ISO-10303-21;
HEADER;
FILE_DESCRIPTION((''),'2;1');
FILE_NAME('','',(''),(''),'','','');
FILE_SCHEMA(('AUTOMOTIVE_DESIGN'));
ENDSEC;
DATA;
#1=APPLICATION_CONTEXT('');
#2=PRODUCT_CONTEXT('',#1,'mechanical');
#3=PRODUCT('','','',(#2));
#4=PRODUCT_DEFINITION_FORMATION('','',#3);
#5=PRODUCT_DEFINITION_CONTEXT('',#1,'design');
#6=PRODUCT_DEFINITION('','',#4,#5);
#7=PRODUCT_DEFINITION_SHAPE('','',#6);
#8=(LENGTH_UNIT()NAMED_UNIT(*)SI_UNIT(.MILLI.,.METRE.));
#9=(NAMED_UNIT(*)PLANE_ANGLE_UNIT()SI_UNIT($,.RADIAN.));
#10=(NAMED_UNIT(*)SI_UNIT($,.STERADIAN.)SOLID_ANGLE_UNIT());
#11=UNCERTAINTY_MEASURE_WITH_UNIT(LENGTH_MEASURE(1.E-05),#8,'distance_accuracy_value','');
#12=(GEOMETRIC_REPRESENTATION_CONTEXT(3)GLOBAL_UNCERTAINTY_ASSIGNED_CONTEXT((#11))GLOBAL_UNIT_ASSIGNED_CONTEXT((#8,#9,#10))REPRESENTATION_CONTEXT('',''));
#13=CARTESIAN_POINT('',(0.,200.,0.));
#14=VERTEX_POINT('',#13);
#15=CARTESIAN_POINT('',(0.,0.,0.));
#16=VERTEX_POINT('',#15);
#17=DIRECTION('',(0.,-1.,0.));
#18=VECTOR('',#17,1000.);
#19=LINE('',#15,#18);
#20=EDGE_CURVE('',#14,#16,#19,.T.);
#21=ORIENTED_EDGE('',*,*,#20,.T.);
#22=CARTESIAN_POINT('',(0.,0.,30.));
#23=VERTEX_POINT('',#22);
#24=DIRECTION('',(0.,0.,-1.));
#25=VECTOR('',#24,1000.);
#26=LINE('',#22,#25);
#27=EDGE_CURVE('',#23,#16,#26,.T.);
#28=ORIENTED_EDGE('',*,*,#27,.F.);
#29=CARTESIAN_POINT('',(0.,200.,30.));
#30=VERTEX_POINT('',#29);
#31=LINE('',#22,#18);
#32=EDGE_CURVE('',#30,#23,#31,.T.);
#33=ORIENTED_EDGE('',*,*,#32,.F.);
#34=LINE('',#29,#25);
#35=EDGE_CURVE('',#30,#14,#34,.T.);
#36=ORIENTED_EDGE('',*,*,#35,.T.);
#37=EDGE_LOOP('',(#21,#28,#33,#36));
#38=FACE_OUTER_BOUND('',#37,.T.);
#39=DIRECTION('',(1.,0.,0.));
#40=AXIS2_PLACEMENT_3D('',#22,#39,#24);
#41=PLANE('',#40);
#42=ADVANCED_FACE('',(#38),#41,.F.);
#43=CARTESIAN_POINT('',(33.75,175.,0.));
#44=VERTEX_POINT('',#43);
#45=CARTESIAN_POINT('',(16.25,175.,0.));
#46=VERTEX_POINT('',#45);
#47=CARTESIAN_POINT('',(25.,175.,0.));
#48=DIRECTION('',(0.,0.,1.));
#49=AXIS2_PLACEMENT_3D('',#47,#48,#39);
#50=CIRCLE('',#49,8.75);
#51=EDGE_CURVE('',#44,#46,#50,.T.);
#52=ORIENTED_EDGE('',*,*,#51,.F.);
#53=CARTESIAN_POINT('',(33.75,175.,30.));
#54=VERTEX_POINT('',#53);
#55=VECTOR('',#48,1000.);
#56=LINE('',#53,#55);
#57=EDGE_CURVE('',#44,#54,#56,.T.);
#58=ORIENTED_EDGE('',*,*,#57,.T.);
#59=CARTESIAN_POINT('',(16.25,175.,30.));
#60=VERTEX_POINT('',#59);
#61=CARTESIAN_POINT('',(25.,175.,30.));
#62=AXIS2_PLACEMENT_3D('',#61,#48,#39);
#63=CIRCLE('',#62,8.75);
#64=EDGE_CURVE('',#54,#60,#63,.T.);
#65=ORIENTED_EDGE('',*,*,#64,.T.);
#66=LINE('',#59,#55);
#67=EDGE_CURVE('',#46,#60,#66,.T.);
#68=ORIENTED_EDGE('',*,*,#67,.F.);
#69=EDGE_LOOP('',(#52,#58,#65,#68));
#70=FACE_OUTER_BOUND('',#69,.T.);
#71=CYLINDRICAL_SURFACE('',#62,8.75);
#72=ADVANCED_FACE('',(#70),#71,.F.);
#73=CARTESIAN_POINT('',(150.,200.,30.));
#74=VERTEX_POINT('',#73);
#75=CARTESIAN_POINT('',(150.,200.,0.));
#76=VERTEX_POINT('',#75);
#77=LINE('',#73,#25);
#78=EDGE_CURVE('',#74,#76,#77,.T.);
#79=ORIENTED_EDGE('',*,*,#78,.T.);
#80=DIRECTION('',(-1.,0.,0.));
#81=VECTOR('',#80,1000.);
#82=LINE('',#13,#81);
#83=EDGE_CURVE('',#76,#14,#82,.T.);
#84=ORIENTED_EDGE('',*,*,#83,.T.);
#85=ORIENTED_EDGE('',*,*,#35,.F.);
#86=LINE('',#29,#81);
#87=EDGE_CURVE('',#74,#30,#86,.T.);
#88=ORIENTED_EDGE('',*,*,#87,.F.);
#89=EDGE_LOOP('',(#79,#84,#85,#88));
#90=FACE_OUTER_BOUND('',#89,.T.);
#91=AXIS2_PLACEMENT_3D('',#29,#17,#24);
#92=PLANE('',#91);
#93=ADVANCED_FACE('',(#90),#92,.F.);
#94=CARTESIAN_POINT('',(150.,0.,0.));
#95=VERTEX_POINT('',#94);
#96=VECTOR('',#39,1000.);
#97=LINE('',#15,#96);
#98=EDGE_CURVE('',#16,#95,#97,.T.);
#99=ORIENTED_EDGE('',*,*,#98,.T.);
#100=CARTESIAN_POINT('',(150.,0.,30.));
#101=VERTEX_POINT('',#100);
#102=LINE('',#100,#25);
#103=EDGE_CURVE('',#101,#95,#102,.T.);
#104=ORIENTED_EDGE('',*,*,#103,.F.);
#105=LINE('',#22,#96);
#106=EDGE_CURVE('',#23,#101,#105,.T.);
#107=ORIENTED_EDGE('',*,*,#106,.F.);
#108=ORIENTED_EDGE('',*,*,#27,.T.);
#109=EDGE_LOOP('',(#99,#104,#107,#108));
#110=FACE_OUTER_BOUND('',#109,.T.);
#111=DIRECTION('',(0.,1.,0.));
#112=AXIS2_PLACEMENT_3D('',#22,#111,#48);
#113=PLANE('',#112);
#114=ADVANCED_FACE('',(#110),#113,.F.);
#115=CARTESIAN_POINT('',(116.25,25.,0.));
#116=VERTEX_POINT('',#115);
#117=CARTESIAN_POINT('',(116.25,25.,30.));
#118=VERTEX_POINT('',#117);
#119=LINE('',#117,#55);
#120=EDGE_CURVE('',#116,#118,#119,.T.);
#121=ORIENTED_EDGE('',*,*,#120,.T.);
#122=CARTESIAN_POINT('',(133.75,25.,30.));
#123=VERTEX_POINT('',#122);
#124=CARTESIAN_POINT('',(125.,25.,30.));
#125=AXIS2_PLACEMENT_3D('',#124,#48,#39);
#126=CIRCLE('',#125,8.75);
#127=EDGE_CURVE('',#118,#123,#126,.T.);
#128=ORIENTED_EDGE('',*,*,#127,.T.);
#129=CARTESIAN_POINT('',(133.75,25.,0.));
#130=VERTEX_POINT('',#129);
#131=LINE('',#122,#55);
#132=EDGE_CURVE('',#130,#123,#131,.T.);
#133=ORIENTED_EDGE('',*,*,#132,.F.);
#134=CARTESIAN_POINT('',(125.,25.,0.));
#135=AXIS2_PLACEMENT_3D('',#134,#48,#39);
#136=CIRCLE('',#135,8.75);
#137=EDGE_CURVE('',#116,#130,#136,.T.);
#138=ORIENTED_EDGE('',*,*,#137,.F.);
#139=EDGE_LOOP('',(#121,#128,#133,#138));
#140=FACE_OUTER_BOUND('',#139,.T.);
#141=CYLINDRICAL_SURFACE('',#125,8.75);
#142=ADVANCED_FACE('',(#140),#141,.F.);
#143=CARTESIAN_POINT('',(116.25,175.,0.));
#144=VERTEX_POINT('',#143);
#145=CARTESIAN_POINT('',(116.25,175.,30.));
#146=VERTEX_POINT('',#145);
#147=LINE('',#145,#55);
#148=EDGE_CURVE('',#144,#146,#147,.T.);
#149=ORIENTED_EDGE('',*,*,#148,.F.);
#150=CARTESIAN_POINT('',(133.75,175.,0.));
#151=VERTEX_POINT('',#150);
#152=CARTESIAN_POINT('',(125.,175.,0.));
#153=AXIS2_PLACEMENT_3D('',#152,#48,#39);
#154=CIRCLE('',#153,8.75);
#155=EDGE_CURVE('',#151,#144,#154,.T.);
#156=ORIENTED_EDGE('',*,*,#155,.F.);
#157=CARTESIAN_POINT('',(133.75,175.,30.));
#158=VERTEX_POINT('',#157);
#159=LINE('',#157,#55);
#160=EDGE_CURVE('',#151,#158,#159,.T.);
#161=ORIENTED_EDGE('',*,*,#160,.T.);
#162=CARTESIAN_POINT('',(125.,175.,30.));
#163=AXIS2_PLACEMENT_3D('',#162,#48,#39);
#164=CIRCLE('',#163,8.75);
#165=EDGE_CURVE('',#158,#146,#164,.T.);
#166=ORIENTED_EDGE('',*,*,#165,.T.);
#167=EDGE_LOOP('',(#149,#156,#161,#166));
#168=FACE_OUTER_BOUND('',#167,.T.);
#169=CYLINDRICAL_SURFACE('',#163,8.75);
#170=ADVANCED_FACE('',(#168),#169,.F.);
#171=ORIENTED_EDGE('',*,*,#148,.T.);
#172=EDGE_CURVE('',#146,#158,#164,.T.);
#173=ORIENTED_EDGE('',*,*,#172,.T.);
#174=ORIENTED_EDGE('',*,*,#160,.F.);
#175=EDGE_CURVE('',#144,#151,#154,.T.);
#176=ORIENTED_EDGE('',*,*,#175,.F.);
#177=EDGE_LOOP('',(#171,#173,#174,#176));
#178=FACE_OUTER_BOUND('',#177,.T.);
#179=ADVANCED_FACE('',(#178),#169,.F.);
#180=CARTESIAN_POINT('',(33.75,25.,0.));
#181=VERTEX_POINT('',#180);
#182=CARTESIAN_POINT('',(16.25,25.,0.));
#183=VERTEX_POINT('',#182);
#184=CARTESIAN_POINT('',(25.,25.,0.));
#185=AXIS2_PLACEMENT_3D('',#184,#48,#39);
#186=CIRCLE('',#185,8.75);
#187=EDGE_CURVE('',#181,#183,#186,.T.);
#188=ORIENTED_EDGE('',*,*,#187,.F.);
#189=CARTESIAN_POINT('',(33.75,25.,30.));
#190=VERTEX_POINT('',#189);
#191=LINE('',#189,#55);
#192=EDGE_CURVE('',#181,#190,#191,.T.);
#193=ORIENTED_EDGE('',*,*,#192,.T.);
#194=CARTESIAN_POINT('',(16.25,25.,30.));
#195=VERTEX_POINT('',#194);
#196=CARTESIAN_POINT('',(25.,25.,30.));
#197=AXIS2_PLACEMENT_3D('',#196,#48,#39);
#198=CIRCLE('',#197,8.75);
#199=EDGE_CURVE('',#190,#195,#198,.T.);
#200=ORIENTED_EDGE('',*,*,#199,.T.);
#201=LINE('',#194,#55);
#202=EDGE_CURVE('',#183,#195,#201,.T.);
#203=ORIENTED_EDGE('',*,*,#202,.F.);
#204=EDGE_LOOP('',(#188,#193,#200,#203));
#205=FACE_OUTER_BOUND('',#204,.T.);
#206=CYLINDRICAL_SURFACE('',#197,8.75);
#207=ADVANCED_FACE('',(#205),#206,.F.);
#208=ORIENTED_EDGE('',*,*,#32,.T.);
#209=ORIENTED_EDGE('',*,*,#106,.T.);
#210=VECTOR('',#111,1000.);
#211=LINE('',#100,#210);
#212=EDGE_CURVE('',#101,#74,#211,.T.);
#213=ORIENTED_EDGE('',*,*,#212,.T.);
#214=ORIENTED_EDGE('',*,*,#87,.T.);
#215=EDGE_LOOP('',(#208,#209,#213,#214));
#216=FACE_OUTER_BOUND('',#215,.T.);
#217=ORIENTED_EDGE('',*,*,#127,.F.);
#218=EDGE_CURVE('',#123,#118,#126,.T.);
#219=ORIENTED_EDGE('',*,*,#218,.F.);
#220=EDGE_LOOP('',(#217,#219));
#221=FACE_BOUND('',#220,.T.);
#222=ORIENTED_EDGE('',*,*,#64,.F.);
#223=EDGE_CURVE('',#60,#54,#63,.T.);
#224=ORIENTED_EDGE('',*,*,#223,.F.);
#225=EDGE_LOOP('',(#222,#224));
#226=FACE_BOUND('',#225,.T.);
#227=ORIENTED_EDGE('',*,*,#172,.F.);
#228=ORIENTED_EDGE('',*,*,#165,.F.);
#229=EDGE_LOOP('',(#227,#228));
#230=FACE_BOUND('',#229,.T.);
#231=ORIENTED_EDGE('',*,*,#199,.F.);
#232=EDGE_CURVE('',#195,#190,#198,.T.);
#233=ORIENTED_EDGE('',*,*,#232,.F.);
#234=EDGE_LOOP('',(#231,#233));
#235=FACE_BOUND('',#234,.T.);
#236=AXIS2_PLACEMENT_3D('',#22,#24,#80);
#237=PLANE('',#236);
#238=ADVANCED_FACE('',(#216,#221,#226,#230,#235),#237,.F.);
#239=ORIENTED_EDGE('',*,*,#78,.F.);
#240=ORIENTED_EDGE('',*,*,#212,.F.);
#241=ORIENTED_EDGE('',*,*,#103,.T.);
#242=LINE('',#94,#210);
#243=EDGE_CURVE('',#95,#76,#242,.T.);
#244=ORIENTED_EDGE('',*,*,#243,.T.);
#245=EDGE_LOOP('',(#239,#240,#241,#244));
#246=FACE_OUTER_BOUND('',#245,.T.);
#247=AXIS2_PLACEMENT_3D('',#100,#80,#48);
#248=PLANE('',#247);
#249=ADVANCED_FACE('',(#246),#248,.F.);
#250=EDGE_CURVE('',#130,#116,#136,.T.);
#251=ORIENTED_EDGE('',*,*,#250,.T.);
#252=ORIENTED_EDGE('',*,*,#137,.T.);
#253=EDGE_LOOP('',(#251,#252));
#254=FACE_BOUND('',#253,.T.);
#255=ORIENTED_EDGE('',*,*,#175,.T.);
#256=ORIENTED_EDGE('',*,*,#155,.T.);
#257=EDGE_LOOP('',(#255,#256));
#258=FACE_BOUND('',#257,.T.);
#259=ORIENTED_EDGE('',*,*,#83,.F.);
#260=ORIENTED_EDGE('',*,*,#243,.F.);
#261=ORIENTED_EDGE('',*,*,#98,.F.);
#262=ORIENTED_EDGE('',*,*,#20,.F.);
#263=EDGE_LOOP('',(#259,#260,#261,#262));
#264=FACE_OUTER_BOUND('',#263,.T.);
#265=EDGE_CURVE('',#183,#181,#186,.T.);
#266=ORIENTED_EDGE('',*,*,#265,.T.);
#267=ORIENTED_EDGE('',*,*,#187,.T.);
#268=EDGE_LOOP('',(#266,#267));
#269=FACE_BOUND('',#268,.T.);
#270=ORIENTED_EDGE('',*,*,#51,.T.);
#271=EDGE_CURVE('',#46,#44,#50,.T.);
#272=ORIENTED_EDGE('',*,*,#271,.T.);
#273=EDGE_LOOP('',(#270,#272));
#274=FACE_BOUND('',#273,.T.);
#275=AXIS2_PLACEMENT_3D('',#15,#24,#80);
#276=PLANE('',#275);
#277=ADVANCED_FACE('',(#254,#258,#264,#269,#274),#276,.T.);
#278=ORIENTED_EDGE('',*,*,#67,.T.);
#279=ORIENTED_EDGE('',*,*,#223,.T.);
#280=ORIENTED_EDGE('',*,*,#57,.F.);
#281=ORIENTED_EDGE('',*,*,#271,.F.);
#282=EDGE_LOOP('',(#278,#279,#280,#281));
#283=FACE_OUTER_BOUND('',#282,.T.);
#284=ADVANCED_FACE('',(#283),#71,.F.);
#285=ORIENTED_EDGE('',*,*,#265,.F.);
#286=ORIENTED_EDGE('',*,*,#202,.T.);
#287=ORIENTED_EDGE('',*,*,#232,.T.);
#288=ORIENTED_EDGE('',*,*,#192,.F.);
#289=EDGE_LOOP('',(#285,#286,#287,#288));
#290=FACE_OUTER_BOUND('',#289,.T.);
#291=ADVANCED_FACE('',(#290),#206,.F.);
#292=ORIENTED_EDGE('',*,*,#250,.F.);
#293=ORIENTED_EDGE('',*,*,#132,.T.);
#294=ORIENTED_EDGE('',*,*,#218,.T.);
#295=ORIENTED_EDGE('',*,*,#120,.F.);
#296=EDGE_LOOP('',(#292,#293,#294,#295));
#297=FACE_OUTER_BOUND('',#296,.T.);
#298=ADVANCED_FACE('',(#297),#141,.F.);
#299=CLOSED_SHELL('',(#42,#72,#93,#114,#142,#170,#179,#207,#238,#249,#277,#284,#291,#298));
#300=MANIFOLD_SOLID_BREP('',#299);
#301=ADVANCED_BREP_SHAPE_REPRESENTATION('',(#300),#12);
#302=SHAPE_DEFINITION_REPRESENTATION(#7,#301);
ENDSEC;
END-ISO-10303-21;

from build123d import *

# Parameters (mm, degrees)
SKETCH1_W            = 150
SKETCH1_H            = 200
BOSS_EXTRUDE1_DEPTH  = 30
M20_THREADED_HOLE1_D = 17.5


with BuildPart() as part:
    # Sketch1 → Boss-Extrude1 (new body)
    with BuildSketch(Plane.XY):
        with Locations((75, 100)):
            Rectangle(SKETCH1_W, SKETCH1_H)
    extrude(amount=BOSS_EXTRUDE1_DEPTH)

    # M20 Threaded hole1 (through all)
    with Locations(Plane(origin=(25, 175, 30), x_dir=(1, 0, 0), z_dir=(0, 0, 1))):
        with Locations((0, 0), (100, 0), (0, -150), (100, -150)):
            Hole(M20_THREADED_HOLE1_D / 2)


solid = part.part
